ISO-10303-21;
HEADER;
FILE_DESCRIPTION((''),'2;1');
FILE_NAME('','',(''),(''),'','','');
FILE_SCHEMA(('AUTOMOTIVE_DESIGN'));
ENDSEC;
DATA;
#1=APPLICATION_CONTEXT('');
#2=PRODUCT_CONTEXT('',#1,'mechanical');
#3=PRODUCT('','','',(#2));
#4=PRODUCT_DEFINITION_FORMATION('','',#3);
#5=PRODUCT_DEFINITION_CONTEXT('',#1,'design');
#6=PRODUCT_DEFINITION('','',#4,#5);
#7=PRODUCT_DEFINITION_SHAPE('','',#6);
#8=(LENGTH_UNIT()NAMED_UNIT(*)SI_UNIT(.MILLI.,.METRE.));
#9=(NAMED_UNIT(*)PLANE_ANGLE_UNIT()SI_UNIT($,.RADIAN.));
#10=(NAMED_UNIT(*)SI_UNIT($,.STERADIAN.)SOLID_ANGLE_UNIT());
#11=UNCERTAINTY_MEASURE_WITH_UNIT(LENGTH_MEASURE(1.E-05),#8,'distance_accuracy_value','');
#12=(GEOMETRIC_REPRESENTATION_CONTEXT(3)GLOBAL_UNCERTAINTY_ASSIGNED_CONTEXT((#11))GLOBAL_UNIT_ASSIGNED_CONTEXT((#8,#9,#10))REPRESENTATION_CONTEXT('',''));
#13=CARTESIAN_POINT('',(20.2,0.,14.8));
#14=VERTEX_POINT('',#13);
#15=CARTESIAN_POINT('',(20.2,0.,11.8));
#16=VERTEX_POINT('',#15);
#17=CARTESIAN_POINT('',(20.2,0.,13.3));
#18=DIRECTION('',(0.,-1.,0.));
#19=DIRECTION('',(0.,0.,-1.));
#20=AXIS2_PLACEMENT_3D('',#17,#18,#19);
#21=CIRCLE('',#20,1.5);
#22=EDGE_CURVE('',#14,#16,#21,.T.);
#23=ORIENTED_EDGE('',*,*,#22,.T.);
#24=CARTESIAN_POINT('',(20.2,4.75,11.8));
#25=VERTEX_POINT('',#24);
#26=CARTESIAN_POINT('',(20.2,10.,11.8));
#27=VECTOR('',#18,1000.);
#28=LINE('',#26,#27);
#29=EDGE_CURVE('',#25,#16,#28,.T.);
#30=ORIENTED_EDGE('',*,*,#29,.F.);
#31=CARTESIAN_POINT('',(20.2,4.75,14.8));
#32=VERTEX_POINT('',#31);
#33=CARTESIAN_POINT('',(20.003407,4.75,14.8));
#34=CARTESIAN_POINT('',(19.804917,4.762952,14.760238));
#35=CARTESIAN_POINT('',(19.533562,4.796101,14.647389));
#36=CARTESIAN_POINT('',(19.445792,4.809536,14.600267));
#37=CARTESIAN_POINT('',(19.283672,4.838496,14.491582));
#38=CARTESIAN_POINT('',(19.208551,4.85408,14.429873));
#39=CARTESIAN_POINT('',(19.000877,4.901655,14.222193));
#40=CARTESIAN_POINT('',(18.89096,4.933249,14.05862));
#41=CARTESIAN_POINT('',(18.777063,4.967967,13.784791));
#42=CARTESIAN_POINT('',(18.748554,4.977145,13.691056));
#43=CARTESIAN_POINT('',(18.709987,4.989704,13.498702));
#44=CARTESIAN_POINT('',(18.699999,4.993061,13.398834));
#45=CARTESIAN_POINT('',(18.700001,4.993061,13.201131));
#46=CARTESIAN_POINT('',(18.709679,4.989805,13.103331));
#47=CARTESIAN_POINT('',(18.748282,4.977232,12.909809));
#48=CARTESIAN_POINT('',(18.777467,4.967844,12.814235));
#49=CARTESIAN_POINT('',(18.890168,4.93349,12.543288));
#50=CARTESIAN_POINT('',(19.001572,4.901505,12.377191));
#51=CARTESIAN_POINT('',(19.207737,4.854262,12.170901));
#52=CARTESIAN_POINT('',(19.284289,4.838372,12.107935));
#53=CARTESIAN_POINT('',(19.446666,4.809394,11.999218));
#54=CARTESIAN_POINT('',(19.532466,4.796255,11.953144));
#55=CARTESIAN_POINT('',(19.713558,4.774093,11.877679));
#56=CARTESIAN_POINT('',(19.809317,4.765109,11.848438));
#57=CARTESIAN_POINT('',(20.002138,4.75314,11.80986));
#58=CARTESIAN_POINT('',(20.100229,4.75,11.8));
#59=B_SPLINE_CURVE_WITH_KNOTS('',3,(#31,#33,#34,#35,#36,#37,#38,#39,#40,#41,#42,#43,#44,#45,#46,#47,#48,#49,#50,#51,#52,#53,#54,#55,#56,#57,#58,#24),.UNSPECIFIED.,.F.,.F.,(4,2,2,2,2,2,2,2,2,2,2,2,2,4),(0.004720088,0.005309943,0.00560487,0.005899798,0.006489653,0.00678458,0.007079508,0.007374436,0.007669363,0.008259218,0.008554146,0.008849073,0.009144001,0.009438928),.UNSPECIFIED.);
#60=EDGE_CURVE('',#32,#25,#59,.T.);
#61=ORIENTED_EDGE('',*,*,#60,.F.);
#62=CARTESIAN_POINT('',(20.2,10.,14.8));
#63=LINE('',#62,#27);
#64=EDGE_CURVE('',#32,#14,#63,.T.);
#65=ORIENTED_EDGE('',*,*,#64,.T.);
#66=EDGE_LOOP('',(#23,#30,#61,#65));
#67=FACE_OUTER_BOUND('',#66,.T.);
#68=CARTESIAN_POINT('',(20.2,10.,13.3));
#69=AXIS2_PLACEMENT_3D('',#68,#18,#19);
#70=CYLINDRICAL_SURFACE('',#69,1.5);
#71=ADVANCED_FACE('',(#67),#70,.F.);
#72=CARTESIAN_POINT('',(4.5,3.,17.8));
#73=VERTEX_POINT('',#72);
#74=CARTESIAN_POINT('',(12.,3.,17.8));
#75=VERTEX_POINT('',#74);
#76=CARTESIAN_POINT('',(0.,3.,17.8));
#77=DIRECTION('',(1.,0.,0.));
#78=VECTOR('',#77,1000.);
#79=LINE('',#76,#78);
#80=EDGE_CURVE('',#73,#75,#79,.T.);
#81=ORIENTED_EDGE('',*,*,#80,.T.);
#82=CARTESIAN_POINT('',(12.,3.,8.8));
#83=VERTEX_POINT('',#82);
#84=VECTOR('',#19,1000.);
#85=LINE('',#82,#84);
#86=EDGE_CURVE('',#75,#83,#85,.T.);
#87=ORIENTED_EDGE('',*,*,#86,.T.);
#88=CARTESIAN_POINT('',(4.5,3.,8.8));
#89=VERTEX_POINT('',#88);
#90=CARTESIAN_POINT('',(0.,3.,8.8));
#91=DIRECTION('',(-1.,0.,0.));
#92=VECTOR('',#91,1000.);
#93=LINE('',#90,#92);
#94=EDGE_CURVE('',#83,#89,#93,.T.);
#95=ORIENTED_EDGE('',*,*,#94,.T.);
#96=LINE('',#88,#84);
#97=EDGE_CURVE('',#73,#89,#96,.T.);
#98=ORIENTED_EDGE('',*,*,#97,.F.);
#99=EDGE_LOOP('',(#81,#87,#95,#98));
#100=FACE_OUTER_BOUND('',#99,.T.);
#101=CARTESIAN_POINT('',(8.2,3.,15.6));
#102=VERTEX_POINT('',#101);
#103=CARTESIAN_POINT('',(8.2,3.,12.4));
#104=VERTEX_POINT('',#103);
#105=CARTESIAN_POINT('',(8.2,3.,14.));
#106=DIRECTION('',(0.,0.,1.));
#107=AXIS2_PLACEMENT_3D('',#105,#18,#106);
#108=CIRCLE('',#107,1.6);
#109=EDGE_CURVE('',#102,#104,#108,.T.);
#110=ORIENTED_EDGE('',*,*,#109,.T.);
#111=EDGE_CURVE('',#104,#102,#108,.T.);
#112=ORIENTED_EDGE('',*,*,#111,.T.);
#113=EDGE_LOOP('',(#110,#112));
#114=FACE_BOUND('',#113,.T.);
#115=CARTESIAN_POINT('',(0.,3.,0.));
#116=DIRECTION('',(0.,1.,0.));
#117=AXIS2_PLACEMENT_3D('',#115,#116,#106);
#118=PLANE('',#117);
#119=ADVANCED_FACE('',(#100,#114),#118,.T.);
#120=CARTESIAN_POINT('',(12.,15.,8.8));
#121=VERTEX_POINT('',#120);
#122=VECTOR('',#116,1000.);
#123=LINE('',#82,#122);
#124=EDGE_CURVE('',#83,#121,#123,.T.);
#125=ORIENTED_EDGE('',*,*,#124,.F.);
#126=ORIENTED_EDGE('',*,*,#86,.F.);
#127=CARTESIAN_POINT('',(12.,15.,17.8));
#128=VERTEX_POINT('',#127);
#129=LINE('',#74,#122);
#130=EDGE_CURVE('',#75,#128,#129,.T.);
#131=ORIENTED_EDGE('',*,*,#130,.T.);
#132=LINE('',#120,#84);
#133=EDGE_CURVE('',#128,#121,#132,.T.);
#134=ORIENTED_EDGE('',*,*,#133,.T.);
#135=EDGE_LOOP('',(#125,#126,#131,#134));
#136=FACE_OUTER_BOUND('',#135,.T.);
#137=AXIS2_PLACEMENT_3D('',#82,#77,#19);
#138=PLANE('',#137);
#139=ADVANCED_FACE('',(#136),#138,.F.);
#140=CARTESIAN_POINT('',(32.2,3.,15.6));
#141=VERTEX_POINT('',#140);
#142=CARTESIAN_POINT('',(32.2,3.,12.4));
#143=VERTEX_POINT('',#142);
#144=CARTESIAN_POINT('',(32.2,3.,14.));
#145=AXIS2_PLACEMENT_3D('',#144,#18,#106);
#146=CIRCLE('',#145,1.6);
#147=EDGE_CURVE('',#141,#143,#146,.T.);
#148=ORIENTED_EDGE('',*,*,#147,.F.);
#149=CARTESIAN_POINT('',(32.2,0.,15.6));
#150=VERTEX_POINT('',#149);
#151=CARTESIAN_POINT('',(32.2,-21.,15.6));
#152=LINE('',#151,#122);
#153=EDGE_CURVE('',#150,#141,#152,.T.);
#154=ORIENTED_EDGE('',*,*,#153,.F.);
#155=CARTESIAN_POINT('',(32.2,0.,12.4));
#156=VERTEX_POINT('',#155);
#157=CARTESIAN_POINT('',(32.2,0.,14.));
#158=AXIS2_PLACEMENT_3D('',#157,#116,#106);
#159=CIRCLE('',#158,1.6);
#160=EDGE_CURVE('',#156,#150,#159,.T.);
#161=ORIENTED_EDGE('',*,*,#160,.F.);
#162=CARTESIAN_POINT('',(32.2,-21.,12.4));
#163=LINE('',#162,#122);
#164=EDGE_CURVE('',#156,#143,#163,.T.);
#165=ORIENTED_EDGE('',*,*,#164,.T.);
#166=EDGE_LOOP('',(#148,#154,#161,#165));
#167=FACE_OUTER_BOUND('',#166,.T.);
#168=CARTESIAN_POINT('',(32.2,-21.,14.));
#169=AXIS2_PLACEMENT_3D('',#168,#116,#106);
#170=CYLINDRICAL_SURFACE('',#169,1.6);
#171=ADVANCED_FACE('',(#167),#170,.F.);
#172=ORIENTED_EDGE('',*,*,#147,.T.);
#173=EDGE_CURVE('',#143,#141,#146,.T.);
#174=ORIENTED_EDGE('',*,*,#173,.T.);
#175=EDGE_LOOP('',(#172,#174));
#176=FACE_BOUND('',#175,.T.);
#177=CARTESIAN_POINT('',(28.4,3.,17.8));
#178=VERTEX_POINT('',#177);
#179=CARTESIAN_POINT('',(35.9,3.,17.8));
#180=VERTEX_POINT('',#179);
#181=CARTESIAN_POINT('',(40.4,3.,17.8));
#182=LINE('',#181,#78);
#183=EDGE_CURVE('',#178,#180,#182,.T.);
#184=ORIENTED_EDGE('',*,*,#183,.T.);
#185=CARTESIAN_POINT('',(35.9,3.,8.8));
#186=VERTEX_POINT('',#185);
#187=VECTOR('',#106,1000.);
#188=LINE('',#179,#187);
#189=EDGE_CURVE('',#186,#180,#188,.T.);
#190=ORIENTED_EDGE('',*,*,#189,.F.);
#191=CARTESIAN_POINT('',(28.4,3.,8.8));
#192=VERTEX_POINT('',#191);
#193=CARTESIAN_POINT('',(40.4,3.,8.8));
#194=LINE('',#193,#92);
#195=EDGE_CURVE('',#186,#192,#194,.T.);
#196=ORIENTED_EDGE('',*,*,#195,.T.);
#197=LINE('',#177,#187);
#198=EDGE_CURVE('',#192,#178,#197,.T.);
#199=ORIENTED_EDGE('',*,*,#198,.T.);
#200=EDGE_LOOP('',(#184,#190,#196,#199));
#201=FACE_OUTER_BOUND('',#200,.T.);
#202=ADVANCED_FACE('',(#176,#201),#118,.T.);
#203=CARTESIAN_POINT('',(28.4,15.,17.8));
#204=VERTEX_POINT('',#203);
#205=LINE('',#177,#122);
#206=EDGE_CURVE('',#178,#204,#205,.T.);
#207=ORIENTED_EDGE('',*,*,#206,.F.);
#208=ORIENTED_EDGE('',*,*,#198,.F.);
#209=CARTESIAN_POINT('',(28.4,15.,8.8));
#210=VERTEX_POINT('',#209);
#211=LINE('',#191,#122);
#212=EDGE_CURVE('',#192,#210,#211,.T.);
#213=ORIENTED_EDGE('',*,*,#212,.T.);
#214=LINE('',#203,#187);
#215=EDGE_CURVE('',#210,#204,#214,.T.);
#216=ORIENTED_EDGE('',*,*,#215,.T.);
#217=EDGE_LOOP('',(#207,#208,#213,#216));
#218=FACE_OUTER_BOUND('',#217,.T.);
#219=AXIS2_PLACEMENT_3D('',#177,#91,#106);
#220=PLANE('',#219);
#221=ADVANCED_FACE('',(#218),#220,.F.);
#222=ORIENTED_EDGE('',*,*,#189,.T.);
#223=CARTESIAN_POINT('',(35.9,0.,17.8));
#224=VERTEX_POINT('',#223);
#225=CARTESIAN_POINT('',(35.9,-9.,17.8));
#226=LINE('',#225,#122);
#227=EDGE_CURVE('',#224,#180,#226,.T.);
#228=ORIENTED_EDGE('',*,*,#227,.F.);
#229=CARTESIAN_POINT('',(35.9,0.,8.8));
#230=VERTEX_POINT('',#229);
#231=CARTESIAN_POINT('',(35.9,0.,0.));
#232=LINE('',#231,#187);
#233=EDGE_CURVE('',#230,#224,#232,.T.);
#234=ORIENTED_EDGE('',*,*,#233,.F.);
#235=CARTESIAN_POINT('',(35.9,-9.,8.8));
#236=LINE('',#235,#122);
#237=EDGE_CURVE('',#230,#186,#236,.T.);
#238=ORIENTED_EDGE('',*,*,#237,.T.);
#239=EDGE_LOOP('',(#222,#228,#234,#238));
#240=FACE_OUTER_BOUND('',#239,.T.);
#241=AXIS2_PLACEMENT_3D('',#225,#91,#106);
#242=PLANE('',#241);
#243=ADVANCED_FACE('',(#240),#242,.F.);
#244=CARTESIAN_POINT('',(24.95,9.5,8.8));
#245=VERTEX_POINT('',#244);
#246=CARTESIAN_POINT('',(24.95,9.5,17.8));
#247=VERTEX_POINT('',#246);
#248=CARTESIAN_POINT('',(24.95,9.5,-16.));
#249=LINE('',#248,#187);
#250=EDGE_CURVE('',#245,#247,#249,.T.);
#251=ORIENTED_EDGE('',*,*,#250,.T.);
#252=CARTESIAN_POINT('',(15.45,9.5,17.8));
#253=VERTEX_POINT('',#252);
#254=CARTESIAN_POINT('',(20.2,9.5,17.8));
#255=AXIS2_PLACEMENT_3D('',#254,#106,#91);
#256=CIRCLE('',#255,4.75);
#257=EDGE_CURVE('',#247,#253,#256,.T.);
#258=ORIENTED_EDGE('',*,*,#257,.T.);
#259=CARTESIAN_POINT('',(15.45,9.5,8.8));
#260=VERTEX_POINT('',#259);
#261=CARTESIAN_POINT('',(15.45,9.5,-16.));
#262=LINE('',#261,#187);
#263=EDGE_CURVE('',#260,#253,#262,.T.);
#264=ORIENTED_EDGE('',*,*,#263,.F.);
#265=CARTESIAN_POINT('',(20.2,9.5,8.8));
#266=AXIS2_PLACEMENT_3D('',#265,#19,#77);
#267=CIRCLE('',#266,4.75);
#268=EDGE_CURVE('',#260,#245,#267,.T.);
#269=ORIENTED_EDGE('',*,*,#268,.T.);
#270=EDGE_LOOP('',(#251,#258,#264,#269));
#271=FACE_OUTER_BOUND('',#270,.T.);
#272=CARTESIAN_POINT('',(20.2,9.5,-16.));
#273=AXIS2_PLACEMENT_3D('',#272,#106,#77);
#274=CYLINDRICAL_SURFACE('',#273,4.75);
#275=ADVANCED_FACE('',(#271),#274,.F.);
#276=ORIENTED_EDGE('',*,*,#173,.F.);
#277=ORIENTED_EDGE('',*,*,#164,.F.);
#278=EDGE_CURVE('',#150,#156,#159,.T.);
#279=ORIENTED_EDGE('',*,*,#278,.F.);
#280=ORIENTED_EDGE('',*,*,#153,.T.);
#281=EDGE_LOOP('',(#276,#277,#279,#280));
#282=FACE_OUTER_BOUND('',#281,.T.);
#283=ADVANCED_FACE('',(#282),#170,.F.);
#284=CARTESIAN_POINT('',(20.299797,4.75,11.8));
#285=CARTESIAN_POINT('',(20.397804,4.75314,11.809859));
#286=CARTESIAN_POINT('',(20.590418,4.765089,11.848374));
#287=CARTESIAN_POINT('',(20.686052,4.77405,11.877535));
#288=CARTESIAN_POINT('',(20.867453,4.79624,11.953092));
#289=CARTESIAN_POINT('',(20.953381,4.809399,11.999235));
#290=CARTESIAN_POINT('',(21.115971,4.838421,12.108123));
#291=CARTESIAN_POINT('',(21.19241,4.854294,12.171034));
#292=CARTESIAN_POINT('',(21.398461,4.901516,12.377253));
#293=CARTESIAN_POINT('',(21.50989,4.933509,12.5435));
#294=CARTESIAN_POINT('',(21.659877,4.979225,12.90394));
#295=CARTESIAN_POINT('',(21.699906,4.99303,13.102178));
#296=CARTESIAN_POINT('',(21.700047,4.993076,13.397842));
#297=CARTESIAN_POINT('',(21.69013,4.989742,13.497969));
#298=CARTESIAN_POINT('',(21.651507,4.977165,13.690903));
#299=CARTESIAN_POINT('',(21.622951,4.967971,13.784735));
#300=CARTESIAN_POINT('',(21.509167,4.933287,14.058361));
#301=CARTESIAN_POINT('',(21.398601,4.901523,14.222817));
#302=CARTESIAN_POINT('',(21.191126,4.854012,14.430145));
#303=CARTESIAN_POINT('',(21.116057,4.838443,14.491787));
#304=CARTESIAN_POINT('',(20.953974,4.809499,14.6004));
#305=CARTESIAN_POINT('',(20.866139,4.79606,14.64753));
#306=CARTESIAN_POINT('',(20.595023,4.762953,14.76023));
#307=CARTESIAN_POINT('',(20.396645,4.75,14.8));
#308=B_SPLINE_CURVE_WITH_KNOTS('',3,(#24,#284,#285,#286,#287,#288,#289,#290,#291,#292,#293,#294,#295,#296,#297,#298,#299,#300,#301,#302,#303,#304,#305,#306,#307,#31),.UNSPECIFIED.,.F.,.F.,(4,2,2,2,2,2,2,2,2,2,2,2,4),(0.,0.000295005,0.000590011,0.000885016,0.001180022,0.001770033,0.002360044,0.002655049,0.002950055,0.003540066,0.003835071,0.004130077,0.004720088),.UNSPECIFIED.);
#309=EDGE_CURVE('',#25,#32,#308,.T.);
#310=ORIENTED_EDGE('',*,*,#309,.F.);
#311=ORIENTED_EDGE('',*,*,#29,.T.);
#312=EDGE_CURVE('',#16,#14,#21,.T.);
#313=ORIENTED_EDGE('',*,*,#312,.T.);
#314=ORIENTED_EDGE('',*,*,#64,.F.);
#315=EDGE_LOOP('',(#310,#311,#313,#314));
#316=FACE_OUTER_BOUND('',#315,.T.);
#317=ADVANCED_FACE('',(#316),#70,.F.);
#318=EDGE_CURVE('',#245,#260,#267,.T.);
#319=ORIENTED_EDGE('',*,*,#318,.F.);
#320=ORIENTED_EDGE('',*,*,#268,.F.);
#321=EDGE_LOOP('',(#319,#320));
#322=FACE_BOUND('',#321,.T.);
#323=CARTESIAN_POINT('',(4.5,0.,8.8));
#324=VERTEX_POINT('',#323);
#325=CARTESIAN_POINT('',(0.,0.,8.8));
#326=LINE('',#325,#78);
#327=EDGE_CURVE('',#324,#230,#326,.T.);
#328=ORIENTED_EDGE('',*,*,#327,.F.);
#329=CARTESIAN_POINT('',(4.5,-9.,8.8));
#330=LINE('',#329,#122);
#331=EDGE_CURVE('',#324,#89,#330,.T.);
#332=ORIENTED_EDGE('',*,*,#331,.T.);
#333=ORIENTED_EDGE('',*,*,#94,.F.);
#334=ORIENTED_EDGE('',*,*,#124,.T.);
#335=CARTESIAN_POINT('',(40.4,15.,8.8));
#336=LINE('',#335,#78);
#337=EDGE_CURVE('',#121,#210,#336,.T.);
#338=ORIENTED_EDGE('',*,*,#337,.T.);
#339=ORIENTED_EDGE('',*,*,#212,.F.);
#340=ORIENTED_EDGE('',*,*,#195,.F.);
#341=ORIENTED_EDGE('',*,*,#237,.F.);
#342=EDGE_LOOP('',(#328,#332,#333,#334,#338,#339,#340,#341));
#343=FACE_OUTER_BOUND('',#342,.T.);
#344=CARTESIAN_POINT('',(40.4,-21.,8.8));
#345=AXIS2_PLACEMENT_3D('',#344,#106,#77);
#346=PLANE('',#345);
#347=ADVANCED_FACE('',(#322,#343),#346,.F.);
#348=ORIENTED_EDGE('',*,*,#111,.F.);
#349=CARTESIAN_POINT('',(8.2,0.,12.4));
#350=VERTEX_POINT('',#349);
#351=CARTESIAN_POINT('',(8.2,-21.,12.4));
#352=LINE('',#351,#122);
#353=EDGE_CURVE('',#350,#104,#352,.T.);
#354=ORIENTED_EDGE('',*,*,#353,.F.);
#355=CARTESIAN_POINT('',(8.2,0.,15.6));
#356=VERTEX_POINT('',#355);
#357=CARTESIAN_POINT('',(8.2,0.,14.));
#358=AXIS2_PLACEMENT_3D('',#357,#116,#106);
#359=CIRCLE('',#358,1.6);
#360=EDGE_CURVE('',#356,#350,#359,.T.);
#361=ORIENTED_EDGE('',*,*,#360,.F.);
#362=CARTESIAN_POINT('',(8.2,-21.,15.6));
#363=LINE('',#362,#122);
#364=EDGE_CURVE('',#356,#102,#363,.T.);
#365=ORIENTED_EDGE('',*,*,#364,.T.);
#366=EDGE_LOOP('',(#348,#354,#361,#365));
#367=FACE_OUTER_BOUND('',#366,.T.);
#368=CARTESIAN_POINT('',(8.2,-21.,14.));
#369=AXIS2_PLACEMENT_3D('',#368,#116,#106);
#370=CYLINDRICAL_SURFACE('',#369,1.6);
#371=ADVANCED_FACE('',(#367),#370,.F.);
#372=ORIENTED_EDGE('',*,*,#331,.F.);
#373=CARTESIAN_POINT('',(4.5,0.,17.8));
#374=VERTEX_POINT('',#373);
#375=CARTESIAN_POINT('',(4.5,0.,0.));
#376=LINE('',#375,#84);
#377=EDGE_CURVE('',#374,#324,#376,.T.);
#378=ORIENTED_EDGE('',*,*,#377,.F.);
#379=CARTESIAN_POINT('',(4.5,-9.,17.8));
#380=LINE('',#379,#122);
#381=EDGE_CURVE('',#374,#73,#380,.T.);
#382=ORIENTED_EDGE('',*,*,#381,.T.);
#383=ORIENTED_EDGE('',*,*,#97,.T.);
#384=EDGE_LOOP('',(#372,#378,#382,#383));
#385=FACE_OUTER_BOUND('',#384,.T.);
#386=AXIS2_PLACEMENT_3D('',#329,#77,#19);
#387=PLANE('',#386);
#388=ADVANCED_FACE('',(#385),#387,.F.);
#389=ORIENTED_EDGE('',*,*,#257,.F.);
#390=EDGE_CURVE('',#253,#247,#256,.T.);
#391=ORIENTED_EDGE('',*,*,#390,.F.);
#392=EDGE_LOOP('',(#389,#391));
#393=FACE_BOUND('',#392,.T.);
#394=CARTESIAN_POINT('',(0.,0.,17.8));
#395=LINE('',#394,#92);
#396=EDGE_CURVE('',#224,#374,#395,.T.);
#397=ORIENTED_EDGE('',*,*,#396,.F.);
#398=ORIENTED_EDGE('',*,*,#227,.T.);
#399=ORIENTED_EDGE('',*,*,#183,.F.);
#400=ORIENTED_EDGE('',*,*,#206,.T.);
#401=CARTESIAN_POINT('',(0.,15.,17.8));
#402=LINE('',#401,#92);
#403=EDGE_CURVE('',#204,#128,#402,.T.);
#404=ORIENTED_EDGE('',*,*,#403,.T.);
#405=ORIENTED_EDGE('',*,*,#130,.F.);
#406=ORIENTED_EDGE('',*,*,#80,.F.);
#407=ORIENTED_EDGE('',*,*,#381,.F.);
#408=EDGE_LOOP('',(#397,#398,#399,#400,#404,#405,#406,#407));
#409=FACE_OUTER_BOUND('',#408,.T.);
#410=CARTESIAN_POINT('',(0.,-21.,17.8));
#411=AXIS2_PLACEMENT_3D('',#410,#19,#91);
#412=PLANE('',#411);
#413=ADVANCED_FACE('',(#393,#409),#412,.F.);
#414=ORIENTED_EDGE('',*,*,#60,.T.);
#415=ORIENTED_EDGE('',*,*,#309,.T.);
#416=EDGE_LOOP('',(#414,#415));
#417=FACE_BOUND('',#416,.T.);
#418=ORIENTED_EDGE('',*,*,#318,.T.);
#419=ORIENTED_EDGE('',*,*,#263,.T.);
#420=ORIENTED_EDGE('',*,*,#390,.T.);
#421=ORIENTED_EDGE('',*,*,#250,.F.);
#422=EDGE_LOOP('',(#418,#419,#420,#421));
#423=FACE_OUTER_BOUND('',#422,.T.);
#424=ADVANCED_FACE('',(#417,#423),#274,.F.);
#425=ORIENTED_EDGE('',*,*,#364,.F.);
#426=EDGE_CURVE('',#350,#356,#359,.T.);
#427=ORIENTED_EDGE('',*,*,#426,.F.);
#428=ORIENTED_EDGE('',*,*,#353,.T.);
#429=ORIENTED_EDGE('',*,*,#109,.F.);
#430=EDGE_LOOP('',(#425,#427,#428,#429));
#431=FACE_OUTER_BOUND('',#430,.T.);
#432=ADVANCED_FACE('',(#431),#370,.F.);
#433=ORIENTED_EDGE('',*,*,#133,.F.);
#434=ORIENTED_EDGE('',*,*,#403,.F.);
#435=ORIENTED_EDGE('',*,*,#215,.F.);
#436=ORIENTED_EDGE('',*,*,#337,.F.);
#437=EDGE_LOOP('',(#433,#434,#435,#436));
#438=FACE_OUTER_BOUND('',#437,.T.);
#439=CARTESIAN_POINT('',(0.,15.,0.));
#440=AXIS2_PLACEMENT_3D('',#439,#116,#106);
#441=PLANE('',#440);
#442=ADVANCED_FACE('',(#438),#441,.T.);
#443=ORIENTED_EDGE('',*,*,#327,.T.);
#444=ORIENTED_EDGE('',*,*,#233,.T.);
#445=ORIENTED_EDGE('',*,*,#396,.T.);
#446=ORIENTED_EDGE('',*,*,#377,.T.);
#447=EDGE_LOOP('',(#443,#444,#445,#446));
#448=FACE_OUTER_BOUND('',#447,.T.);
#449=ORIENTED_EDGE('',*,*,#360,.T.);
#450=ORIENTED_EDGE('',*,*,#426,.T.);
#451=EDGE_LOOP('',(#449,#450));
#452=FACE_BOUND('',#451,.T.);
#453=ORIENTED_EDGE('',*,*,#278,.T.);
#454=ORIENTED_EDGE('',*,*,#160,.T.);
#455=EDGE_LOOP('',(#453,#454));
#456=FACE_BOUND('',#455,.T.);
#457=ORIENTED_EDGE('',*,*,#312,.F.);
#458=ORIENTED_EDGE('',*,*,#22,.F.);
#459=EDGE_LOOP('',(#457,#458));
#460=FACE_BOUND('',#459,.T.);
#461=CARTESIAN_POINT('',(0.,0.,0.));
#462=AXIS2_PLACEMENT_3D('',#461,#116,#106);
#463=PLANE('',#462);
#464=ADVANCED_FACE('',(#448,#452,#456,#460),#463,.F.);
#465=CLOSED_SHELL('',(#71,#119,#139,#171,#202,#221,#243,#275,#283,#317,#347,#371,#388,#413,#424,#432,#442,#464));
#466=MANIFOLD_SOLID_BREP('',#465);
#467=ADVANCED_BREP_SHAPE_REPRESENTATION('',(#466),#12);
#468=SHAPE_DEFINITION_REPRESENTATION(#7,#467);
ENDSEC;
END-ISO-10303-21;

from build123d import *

# Parameters (mm, degrees)
SKETCH1_W           = 40.4
SKETCH1_H           = 20
BOSS_EXTRUDE1_DEPTH = 15
SKETCH2_R           = 4.75
CUT_EXTRUDE1_DEPTH  = 36
SKETCH3_R           = 1.6
CUT_EXTRUDE2_DEPTH  = 36
SKETCH4_W           = 40.4
SKETCH4_H           = 8.8
CUT_EXTRUDE3_DEPTH  = 36
SKETCH5_W           = 40.4
SKETCH5_H           = 2.2
CUT_EXTRUDE4_DEPTH  = 36
SKETCH8_W           = 12
SKETCH8_H           = 9
CUT_EXTRUDE6_DEPTH  = 12
SKETCH10_W          = 4.5
SKETCH10_H          = 9
CUT_EXTRUDE7_DEPTH  = 12
SKETCH11_R          = 1.5
CUT_EXTRUDE8_DEPTH  = 10


with BuildPart() as part:
    # Sketch1 → Boss-Extrude1 (new body)
    with BuildSketch(Plane(origin=(0, 0, 0), x_dir=(1, 0, 0), z_dir=(0, 1, 0))):
        with Locations((20.2, -10)):
            Rectangle(SKETCH1_W, SKETCH1_H)
    extrude(amount=BOSS_EXTRUDE1_DEPTH)

    # Sketch2 → Cut-Extrude1 (cut)
    with BuildSketch(Plane.XY.offset(20)):
        with Locations((20.2, 9.5)):
            Circle(SKETCH2_R)
    extrude(amount=-CUT_EXTRUDE1_DEPTH, mode=Mode.SUBTRACT)

    # Sketch3 → Cut-Extrude2 (cut)
    with BuildSketch(Plane(origin=(0, 15, 0), x_dir=(1, 0, 0), z_dir=(0, 1, 0))):
        with Locations(Location((8.2, -14, 0), (0, 0, 270))):
            Circle(SKETCH3_R)
        with Locations(Location((32.2, -14, 0), (0, 0, 270))):
            Circle(SKETCH3_R)
    extrude(amount=-CUT_EXTRUDE2_DEPTH, mode=Mode.SUBTRACT)

    # Sketch4 → Cut-Extrude3 (cut)
    with BuildSketch(Plane(origin=(0, 15, 0), x_dir=(1, 0, 0), z_dir=(0, 1, 0))):
        with Locations((20.2, -4.4)):
            Rectangle(SKETCH4_W, SKETCH4_H)
    extrude(amount=-CUT_EXTRUDE3_DEPTH, mode=Mode.SUBTRACT)

    # Sketch5 → Cut-Extrude4 (cut)
    with BuildSketch(Plane(origin=(0, 15, 0), x_dir=(1, 0, 0), z_dir=(0, 1, 0))):
        with Locations((20.2, -18.9)):
            Rectangle(SKETCH5_W, SKETCH5_H)
    extrude(amount=-CUT_EXTRUDE4_DEPTH, mode=Mode.SUBTRACT)

    # Sketch8 → Cut-Extrude6 (cut)
    with BuildSketch(Plane(origin=(0, 15, 0), x_dir=(1, 0, 0), z_dir=(0, 1, 0))):
        with Locations((6, -13.3)):
            Rectangle(SKETCH8_W, SKETCH8_H)
        with Locations((34.4, -13.3)):
            Rectangle(SKETCH8_W, SKETCH8_H)
    extrude(amount=-CUT_EXTRUDE6_DEPTH, mode=Mode.SUBTRACT)

    # Sketch10 → Cut-Extrude7 (cut)
    with BuildSketch(Plane(origin=(0, 3, 0), x_dir=(1, 0, 0), z_dir=(0, 1, 0))):
        with Locations((2.25, -13.3)):
            Rectangle(SKETCH10_W, SKETCH10_H)
        with Locations((38.15, -13.3)):
            Rectangle(SKETCH10_W, SKETCH10_H)
    extrude(amount=-CUT_EXTRUDE7_DEPTH, mode=Mode.SUBTRACT)

    # Sketch11 → Cut-Extrude8 (cut)
    with BuildSketch(Plane.XZ):
        with Locations(Location((20.2, 13.3, 0), (0, 0, 270))):
            Circle(SKETCH11_R)
    extrude(amount=-CUT_EXTRUDE8_DEPTH, mode=Mode.SUBTRACT)


solid = part.part
